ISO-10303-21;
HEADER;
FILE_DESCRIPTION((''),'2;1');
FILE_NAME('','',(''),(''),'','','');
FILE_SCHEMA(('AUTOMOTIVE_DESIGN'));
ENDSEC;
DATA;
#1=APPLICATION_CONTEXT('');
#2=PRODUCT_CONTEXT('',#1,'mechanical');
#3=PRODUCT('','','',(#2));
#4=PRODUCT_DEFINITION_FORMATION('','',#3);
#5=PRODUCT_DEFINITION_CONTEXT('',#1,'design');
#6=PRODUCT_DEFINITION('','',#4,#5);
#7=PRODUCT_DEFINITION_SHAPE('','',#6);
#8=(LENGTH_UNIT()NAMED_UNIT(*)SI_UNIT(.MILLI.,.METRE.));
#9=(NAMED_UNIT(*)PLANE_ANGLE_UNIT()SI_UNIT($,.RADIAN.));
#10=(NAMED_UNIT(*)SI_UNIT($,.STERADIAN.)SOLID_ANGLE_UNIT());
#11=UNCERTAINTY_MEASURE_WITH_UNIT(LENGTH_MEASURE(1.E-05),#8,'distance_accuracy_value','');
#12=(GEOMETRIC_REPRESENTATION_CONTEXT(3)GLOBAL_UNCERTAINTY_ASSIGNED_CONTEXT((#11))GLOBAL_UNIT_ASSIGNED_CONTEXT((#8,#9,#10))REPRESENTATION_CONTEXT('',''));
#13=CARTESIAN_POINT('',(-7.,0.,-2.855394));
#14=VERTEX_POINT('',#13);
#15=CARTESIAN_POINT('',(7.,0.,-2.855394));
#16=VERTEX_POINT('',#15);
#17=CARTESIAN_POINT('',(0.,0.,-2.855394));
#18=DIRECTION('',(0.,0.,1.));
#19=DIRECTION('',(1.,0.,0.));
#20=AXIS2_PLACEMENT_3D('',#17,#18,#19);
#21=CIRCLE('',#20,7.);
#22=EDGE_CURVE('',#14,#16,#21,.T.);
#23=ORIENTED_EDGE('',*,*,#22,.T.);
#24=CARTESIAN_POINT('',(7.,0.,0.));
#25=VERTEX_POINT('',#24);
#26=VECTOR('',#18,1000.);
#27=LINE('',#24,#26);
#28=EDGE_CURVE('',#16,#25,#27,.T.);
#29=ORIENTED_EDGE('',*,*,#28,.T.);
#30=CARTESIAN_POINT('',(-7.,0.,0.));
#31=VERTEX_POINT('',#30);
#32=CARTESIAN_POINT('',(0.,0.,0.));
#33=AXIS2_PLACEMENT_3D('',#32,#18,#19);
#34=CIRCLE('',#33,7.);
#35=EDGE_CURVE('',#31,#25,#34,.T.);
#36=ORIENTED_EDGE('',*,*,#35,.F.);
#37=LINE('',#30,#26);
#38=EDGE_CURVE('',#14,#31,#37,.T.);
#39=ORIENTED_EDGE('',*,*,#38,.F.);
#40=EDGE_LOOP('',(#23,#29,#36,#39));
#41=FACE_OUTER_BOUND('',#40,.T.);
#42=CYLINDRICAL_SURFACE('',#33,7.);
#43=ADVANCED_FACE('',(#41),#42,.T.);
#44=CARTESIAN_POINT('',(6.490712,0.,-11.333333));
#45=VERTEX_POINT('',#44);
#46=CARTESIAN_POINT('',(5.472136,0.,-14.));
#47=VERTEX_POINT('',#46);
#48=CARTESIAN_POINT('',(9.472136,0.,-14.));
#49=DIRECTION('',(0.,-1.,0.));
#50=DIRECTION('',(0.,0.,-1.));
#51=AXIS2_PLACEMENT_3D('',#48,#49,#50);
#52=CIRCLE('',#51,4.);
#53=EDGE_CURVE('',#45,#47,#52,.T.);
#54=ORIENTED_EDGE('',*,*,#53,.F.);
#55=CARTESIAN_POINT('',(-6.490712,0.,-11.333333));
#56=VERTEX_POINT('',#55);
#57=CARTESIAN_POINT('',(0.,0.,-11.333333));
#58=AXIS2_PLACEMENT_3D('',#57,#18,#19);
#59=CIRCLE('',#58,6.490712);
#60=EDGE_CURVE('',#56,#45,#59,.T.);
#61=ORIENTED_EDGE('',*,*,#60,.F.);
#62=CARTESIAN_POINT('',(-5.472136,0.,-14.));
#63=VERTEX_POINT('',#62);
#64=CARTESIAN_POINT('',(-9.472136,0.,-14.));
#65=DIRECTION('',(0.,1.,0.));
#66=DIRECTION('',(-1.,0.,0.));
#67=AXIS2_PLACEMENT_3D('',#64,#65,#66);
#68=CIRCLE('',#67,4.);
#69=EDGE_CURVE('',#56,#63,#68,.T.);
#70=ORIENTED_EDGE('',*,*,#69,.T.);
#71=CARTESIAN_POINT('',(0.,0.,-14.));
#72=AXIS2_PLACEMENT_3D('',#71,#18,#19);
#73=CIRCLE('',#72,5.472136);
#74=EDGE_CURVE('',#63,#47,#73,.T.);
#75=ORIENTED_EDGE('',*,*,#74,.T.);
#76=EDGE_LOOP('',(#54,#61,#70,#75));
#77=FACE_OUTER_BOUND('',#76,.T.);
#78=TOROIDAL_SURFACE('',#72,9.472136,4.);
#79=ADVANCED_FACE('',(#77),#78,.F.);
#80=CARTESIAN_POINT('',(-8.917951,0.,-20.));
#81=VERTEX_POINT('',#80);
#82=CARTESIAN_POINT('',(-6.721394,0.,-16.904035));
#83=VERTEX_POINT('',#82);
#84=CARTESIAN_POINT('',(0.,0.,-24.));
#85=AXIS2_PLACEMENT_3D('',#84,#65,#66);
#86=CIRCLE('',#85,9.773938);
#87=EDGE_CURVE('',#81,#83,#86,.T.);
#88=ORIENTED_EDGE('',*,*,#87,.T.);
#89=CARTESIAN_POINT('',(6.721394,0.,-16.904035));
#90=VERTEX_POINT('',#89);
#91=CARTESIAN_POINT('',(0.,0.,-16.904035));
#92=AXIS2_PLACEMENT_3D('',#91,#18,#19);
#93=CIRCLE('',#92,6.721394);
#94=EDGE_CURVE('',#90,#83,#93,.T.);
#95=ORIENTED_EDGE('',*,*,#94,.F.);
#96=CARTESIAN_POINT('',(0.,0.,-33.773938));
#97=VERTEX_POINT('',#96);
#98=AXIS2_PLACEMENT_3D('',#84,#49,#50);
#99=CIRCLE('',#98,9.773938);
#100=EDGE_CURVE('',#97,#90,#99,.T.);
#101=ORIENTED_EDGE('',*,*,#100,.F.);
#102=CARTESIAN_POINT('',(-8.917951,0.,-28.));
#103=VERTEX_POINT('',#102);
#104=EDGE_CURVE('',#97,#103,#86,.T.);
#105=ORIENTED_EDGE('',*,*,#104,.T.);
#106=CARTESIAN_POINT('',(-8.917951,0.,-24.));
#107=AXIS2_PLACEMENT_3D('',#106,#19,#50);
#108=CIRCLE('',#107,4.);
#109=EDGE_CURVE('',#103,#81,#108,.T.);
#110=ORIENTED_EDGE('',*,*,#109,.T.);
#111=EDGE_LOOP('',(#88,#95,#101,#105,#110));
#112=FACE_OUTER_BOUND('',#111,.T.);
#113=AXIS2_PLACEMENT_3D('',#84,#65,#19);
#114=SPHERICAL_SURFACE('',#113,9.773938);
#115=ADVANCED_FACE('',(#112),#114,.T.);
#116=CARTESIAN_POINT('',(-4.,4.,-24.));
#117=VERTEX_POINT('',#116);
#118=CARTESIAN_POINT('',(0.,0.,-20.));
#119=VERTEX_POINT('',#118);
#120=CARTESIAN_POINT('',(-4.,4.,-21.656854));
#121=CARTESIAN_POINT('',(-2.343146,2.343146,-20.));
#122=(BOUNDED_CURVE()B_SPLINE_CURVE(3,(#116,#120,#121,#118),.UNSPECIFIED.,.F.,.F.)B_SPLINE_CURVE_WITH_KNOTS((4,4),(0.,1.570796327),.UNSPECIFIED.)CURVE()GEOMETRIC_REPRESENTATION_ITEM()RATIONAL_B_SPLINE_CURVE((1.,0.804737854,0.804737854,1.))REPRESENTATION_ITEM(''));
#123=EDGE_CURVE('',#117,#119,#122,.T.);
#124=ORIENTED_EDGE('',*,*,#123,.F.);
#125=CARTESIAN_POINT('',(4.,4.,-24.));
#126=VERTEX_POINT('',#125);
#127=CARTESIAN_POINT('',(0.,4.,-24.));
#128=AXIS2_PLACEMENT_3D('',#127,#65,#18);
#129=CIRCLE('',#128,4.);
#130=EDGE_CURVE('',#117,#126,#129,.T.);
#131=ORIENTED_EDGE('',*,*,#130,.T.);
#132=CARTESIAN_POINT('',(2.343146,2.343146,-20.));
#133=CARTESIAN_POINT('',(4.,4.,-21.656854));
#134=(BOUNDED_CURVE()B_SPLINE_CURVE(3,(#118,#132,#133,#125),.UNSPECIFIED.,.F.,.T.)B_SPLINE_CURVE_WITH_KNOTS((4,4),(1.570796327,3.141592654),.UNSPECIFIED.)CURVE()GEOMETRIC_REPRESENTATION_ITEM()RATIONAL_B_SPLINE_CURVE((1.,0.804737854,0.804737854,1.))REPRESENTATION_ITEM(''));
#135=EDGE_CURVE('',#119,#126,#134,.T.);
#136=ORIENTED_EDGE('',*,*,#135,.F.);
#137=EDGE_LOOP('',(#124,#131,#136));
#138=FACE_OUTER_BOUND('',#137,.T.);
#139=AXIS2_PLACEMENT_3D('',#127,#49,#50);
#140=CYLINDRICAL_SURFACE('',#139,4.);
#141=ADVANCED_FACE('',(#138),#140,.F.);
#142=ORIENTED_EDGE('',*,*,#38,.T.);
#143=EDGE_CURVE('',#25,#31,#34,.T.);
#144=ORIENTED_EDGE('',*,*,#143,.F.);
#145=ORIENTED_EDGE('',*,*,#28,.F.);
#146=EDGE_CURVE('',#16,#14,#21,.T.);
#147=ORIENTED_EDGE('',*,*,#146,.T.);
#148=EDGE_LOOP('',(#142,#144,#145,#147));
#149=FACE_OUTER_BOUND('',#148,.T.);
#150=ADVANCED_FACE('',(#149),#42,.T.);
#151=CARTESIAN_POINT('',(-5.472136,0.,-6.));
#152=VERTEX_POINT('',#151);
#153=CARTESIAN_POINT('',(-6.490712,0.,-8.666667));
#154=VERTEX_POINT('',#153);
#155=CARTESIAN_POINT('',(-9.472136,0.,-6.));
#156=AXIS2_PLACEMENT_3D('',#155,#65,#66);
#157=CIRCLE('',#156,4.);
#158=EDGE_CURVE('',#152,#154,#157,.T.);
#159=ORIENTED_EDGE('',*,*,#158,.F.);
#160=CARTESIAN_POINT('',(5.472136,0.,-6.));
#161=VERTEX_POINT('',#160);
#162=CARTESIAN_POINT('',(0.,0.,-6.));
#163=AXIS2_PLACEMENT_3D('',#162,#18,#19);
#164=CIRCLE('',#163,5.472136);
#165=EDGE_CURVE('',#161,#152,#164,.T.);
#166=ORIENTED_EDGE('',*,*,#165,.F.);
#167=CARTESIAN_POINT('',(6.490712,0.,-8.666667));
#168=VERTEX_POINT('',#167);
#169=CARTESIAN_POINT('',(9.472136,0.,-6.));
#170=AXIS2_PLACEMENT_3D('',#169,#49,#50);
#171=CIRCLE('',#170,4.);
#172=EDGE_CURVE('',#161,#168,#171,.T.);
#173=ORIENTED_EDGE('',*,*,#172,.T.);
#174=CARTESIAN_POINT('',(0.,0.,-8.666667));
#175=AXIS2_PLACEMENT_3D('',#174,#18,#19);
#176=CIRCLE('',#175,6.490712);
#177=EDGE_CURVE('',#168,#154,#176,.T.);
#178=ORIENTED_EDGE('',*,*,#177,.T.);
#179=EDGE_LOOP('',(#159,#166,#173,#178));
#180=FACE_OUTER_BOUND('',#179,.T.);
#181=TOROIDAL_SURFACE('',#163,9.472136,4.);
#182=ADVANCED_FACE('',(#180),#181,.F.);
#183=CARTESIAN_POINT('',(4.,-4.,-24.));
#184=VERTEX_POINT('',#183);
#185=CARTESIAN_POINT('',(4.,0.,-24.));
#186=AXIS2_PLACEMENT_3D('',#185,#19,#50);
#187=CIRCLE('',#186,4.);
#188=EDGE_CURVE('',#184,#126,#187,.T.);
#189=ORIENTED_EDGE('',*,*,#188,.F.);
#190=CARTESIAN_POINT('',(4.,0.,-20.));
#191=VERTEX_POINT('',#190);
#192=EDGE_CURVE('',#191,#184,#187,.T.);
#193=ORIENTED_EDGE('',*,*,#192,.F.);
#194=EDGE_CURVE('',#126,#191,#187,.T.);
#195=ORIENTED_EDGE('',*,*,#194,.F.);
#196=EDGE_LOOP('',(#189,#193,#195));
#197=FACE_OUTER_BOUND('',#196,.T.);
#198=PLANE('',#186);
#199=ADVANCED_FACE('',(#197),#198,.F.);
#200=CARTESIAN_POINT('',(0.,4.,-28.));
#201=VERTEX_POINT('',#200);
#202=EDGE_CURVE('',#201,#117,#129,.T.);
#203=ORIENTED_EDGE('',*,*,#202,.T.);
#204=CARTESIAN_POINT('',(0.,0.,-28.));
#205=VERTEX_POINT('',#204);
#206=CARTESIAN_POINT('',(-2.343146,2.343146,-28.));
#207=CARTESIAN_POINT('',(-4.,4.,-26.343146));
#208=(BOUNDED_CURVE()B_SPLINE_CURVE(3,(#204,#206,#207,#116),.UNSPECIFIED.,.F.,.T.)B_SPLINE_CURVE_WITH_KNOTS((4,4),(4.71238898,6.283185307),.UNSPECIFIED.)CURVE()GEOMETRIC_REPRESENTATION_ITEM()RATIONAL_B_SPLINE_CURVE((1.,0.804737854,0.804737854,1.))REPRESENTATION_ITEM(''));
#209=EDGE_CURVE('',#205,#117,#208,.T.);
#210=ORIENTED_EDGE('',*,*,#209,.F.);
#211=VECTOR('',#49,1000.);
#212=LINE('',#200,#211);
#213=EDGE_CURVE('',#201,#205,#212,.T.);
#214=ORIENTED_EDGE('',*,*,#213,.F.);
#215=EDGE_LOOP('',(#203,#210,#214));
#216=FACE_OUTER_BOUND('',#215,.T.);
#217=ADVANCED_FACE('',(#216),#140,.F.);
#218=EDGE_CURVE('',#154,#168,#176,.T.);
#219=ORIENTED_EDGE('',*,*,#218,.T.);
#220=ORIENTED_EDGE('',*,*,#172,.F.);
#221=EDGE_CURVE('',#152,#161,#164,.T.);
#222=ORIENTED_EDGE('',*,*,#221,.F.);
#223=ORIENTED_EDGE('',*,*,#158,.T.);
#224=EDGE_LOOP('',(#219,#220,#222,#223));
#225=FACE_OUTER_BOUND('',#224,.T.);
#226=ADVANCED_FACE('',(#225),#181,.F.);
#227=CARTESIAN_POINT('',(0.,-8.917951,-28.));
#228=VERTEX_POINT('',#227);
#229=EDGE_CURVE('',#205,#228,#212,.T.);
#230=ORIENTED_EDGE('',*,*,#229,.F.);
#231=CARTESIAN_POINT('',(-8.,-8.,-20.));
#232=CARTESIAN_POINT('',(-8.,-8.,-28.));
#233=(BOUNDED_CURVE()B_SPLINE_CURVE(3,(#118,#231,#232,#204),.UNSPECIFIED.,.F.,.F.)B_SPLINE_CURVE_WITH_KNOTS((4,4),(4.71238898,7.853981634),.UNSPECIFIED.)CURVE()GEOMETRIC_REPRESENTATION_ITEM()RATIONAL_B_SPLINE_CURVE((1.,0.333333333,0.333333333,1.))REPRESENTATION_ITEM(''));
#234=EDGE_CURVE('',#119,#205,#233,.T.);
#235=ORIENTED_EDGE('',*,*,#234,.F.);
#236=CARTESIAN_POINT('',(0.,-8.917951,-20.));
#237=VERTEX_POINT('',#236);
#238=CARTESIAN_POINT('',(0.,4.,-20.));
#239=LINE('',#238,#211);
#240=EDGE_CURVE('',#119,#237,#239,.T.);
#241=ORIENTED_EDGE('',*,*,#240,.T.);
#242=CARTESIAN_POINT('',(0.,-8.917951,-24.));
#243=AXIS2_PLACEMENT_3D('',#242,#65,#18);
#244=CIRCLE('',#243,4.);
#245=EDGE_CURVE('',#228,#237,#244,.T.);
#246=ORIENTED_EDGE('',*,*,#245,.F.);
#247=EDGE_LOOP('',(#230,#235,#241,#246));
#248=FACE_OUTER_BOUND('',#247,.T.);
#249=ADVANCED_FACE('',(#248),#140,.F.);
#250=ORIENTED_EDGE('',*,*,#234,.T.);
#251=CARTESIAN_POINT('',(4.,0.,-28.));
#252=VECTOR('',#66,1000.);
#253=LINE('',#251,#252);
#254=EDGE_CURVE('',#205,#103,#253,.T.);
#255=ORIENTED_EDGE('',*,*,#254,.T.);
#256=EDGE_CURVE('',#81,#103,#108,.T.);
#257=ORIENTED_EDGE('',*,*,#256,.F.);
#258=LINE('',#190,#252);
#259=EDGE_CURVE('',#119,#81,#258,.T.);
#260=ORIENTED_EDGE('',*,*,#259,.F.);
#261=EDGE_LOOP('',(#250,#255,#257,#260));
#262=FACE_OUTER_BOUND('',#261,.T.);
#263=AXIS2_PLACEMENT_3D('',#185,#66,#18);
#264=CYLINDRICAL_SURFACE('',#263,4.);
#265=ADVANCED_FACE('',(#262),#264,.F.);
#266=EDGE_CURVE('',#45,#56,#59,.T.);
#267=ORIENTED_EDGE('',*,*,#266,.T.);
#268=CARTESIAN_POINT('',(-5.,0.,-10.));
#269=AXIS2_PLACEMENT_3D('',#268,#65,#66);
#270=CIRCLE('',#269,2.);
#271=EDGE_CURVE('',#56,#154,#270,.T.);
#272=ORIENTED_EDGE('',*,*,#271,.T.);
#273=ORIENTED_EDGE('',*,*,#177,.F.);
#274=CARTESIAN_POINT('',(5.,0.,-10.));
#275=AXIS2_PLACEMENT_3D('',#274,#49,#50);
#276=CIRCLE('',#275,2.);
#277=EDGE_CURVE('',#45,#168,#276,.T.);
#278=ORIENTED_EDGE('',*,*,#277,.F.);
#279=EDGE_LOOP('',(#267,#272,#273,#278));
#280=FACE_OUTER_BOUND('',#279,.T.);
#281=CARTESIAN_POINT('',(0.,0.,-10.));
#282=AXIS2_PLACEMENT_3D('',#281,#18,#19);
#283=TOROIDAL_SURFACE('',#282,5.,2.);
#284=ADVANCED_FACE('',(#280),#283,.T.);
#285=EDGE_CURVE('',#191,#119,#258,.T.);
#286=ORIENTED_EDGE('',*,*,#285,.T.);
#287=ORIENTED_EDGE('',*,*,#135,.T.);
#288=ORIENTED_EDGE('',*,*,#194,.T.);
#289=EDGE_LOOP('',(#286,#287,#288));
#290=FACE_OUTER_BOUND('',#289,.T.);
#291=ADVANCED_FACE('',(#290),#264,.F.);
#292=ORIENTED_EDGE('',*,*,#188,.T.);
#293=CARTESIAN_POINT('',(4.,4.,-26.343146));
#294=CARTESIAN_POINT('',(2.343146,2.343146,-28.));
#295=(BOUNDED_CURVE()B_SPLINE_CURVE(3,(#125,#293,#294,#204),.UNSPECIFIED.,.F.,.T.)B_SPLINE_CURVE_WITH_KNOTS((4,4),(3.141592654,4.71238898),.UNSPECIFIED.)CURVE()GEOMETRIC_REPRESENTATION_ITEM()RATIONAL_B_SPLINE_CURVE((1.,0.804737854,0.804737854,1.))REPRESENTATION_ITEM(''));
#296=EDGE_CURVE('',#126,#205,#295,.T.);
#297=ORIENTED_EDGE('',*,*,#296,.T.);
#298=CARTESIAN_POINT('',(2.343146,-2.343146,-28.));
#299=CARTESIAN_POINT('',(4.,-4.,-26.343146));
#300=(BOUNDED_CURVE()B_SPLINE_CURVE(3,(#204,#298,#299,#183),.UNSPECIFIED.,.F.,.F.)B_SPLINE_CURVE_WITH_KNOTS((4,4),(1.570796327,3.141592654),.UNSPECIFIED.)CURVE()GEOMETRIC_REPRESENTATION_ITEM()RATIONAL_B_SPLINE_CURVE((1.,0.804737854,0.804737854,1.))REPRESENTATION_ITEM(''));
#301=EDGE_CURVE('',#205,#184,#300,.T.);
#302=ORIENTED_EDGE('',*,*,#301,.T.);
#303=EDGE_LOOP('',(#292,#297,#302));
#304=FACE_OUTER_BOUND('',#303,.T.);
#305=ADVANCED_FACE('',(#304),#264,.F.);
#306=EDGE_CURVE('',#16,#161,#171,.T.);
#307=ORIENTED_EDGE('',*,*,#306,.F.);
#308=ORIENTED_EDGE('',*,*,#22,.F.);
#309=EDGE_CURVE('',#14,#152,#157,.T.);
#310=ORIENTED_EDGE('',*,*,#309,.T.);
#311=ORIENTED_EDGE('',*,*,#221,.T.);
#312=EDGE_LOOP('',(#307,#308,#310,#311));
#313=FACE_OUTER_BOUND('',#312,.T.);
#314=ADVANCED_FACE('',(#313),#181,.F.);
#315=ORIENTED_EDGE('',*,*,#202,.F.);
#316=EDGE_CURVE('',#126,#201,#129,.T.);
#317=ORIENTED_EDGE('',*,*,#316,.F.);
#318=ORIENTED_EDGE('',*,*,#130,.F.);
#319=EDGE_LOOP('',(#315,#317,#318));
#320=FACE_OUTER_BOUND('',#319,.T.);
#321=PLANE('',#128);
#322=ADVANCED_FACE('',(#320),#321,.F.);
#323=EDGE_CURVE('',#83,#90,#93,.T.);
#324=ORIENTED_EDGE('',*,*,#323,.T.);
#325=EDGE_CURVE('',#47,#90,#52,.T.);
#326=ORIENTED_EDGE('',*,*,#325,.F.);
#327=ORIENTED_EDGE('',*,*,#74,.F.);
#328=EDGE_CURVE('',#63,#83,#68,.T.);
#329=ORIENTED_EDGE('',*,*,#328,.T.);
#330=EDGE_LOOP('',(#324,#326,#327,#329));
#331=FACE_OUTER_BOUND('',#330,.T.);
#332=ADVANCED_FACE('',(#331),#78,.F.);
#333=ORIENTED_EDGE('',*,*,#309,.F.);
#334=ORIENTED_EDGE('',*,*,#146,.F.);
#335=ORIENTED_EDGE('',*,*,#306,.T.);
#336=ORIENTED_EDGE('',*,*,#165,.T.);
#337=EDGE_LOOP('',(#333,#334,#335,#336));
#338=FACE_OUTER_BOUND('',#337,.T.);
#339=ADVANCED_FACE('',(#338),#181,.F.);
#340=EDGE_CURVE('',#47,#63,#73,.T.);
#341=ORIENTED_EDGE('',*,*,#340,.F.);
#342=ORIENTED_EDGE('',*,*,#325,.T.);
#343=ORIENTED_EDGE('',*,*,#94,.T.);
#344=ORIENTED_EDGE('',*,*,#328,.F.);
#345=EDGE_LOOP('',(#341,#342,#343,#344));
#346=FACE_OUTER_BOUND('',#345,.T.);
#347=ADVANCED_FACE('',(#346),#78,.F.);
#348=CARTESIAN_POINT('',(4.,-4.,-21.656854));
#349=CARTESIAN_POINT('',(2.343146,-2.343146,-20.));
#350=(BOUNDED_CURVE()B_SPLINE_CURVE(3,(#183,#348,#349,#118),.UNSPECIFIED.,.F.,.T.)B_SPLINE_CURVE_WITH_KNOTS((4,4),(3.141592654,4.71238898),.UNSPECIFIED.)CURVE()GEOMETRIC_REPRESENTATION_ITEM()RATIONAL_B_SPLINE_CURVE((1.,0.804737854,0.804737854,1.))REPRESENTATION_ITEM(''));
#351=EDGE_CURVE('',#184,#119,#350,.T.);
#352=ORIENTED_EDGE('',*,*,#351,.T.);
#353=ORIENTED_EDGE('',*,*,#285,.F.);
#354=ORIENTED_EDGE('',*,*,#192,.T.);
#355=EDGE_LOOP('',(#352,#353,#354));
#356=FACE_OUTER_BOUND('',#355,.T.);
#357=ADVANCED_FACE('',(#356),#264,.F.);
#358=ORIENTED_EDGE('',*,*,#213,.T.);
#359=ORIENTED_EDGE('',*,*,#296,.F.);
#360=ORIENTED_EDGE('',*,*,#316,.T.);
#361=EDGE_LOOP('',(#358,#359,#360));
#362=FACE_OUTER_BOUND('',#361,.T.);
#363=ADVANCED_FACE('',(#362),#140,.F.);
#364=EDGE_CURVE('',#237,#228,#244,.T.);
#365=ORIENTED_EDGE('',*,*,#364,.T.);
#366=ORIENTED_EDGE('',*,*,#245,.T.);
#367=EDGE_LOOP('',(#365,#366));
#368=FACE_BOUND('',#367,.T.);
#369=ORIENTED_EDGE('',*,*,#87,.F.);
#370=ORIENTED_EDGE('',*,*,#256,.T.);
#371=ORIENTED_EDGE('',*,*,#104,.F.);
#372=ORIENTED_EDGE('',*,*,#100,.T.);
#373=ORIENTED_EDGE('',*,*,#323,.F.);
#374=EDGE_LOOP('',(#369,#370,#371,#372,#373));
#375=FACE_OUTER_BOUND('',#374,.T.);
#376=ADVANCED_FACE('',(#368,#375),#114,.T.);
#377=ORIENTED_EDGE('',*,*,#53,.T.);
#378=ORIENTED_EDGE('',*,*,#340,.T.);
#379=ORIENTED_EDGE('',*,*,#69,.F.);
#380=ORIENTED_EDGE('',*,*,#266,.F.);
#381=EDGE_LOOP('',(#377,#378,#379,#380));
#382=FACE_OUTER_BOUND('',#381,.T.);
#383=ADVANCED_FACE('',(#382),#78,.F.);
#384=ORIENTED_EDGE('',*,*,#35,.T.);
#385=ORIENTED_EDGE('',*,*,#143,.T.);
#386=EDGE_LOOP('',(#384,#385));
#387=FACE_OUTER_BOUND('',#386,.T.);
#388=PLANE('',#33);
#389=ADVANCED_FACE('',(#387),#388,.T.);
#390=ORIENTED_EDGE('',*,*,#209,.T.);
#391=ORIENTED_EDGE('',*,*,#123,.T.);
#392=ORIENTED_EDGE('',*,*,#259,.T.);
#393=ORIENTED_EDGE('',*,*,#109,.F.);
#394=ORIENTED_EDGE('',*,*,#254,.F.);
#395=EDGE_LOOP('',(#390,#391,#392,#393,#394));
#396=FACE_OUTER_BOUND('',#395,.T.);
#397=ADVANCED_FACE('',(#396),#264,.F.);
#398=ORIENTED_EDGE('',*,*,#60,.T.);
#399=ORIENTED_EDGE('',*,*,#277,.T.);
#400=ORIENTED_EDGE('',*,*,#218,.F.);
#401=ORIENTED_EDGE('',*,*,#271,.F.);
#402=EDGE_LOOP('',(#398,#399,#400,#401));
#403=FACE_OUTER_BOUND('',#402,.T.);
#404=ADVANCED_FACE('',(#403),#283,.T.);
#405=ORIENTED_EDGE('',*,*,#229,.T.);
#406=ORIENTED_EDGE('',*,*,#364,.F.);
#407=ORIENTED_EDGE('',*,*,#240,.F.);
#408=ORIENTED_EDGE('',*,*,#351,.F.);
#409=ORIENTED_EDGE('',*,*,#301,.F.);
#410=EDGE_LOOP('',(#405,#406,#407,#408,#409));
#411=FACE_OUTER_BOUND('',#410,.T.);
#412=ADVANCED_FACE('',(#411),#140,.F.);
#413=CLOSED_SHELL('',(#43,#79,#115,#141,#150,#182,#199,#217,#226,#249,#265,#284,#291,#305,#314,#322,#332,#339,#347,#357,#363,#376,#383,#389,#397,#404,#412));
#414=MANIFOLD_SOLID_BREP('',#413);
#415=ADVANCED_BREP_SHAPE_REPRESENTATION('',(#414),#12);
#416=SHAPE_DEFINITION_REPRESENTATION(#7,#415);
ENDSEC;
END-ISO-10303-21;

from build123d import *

# Parameters (mm, degrees)
SIDE_CUT_8_DEPTH_4_DEPTH             = 4
SIDE_CUT_8_DEPTH_4_DEPTH_BACK        = 37.492993619
SIDE_CUT_8_SKETCH_RIGHT_PLANE_R      = 4
CROSS_CUT_8_TWO_DIRECTION_DEPTH      = 4
CROSS_CUT_8_TWO_DIRECTION_DEPTH_BACK = 10
CROSS_CUT_8_SKETCH_TOP_PLANE_R       = 4


with BuildPart() as part:
    # Knob Profile Sketch → Knob Body Revolve (revolve)
    with BuildSketch(Plane(origin=(0, 0, 0), x_dir=(1, 0, 0), z_dir=(0, 1, 0))):
        with BuildLine():
            Line((0, 0), (0, 33.773937692))
            ThreePointArc((0, 33.773937692), (9.079795586, 27.617619401), (6.721394325, 16.904035207))
            ThreePointArc((6.721394325, 16.904035207), (5.475561114, 14.165497859), (6.490711985, 11.333333333))
            ThreePointArc((6.490711985, 11.333333333), (7, 10), (6.490711985, 8.666666667))
            ThreePointArc((6.490711985, 8.666666667), (5.487408857, 5.650786662), (7, 2.855394489))
            Line((7, 2.855394489), (7, 0))
            Line((7, 0), (0, 0))
        make_face()
    revolve(axis=Axis((0, 0, 0), (0, 0, -1)))

    # Side Cut _8 Sketch _Right Plane → Side Cut _8 Depth 4 (cut, two sides: drawn at the far end of the back side and taken through both)
    with BuildSketch(Plane(origin=(0, 0, 0), x_dir=(0, 0, -1), z_dir=(1, 0, 0)).offset(-SIDE_CUT_8_DEPTH_4_DEPTH_BACK)):
        with Locations((24, 0)):
            Circle(SIDE_CUT_8_SKETCH_RIGHT_PLANE_R)
    extrude(amount=SIDE_CUT_8_DEPTH_4_DEPTH + SIDE_CUT_8_DEPTH_4_DEPTH_BACK, mode=Mode.SUBTRACT)

    # Cross Cut _8 Sketch _Top Plane → Cross Cut _8 Two-Direction (cut, two sides: drawn at the far end of the back side and taken through both)
    with BuildSketch(Plane(origin=(0, 0, 0), x_dir=(1, 0, 0), z_dir=(0, 1, 0)).offset(-CROSS_CUT_8_TWO_DIRECTION_DEPTH_BACK)):
        with Locations(Location((0, 24, 0), (0, 0, 270))):
            Circle(CROSS_CUT_8_SKETCH_TOP_PLANE_R)
    extrude(amount=CROSS_CUT_8_TWO_DIRECTION_DEPTH + CROSS_CUT_8_TWO_DIRECTION_DEPTH_BACK, mode=Mode.SUBTRACT)


solid = part.part
